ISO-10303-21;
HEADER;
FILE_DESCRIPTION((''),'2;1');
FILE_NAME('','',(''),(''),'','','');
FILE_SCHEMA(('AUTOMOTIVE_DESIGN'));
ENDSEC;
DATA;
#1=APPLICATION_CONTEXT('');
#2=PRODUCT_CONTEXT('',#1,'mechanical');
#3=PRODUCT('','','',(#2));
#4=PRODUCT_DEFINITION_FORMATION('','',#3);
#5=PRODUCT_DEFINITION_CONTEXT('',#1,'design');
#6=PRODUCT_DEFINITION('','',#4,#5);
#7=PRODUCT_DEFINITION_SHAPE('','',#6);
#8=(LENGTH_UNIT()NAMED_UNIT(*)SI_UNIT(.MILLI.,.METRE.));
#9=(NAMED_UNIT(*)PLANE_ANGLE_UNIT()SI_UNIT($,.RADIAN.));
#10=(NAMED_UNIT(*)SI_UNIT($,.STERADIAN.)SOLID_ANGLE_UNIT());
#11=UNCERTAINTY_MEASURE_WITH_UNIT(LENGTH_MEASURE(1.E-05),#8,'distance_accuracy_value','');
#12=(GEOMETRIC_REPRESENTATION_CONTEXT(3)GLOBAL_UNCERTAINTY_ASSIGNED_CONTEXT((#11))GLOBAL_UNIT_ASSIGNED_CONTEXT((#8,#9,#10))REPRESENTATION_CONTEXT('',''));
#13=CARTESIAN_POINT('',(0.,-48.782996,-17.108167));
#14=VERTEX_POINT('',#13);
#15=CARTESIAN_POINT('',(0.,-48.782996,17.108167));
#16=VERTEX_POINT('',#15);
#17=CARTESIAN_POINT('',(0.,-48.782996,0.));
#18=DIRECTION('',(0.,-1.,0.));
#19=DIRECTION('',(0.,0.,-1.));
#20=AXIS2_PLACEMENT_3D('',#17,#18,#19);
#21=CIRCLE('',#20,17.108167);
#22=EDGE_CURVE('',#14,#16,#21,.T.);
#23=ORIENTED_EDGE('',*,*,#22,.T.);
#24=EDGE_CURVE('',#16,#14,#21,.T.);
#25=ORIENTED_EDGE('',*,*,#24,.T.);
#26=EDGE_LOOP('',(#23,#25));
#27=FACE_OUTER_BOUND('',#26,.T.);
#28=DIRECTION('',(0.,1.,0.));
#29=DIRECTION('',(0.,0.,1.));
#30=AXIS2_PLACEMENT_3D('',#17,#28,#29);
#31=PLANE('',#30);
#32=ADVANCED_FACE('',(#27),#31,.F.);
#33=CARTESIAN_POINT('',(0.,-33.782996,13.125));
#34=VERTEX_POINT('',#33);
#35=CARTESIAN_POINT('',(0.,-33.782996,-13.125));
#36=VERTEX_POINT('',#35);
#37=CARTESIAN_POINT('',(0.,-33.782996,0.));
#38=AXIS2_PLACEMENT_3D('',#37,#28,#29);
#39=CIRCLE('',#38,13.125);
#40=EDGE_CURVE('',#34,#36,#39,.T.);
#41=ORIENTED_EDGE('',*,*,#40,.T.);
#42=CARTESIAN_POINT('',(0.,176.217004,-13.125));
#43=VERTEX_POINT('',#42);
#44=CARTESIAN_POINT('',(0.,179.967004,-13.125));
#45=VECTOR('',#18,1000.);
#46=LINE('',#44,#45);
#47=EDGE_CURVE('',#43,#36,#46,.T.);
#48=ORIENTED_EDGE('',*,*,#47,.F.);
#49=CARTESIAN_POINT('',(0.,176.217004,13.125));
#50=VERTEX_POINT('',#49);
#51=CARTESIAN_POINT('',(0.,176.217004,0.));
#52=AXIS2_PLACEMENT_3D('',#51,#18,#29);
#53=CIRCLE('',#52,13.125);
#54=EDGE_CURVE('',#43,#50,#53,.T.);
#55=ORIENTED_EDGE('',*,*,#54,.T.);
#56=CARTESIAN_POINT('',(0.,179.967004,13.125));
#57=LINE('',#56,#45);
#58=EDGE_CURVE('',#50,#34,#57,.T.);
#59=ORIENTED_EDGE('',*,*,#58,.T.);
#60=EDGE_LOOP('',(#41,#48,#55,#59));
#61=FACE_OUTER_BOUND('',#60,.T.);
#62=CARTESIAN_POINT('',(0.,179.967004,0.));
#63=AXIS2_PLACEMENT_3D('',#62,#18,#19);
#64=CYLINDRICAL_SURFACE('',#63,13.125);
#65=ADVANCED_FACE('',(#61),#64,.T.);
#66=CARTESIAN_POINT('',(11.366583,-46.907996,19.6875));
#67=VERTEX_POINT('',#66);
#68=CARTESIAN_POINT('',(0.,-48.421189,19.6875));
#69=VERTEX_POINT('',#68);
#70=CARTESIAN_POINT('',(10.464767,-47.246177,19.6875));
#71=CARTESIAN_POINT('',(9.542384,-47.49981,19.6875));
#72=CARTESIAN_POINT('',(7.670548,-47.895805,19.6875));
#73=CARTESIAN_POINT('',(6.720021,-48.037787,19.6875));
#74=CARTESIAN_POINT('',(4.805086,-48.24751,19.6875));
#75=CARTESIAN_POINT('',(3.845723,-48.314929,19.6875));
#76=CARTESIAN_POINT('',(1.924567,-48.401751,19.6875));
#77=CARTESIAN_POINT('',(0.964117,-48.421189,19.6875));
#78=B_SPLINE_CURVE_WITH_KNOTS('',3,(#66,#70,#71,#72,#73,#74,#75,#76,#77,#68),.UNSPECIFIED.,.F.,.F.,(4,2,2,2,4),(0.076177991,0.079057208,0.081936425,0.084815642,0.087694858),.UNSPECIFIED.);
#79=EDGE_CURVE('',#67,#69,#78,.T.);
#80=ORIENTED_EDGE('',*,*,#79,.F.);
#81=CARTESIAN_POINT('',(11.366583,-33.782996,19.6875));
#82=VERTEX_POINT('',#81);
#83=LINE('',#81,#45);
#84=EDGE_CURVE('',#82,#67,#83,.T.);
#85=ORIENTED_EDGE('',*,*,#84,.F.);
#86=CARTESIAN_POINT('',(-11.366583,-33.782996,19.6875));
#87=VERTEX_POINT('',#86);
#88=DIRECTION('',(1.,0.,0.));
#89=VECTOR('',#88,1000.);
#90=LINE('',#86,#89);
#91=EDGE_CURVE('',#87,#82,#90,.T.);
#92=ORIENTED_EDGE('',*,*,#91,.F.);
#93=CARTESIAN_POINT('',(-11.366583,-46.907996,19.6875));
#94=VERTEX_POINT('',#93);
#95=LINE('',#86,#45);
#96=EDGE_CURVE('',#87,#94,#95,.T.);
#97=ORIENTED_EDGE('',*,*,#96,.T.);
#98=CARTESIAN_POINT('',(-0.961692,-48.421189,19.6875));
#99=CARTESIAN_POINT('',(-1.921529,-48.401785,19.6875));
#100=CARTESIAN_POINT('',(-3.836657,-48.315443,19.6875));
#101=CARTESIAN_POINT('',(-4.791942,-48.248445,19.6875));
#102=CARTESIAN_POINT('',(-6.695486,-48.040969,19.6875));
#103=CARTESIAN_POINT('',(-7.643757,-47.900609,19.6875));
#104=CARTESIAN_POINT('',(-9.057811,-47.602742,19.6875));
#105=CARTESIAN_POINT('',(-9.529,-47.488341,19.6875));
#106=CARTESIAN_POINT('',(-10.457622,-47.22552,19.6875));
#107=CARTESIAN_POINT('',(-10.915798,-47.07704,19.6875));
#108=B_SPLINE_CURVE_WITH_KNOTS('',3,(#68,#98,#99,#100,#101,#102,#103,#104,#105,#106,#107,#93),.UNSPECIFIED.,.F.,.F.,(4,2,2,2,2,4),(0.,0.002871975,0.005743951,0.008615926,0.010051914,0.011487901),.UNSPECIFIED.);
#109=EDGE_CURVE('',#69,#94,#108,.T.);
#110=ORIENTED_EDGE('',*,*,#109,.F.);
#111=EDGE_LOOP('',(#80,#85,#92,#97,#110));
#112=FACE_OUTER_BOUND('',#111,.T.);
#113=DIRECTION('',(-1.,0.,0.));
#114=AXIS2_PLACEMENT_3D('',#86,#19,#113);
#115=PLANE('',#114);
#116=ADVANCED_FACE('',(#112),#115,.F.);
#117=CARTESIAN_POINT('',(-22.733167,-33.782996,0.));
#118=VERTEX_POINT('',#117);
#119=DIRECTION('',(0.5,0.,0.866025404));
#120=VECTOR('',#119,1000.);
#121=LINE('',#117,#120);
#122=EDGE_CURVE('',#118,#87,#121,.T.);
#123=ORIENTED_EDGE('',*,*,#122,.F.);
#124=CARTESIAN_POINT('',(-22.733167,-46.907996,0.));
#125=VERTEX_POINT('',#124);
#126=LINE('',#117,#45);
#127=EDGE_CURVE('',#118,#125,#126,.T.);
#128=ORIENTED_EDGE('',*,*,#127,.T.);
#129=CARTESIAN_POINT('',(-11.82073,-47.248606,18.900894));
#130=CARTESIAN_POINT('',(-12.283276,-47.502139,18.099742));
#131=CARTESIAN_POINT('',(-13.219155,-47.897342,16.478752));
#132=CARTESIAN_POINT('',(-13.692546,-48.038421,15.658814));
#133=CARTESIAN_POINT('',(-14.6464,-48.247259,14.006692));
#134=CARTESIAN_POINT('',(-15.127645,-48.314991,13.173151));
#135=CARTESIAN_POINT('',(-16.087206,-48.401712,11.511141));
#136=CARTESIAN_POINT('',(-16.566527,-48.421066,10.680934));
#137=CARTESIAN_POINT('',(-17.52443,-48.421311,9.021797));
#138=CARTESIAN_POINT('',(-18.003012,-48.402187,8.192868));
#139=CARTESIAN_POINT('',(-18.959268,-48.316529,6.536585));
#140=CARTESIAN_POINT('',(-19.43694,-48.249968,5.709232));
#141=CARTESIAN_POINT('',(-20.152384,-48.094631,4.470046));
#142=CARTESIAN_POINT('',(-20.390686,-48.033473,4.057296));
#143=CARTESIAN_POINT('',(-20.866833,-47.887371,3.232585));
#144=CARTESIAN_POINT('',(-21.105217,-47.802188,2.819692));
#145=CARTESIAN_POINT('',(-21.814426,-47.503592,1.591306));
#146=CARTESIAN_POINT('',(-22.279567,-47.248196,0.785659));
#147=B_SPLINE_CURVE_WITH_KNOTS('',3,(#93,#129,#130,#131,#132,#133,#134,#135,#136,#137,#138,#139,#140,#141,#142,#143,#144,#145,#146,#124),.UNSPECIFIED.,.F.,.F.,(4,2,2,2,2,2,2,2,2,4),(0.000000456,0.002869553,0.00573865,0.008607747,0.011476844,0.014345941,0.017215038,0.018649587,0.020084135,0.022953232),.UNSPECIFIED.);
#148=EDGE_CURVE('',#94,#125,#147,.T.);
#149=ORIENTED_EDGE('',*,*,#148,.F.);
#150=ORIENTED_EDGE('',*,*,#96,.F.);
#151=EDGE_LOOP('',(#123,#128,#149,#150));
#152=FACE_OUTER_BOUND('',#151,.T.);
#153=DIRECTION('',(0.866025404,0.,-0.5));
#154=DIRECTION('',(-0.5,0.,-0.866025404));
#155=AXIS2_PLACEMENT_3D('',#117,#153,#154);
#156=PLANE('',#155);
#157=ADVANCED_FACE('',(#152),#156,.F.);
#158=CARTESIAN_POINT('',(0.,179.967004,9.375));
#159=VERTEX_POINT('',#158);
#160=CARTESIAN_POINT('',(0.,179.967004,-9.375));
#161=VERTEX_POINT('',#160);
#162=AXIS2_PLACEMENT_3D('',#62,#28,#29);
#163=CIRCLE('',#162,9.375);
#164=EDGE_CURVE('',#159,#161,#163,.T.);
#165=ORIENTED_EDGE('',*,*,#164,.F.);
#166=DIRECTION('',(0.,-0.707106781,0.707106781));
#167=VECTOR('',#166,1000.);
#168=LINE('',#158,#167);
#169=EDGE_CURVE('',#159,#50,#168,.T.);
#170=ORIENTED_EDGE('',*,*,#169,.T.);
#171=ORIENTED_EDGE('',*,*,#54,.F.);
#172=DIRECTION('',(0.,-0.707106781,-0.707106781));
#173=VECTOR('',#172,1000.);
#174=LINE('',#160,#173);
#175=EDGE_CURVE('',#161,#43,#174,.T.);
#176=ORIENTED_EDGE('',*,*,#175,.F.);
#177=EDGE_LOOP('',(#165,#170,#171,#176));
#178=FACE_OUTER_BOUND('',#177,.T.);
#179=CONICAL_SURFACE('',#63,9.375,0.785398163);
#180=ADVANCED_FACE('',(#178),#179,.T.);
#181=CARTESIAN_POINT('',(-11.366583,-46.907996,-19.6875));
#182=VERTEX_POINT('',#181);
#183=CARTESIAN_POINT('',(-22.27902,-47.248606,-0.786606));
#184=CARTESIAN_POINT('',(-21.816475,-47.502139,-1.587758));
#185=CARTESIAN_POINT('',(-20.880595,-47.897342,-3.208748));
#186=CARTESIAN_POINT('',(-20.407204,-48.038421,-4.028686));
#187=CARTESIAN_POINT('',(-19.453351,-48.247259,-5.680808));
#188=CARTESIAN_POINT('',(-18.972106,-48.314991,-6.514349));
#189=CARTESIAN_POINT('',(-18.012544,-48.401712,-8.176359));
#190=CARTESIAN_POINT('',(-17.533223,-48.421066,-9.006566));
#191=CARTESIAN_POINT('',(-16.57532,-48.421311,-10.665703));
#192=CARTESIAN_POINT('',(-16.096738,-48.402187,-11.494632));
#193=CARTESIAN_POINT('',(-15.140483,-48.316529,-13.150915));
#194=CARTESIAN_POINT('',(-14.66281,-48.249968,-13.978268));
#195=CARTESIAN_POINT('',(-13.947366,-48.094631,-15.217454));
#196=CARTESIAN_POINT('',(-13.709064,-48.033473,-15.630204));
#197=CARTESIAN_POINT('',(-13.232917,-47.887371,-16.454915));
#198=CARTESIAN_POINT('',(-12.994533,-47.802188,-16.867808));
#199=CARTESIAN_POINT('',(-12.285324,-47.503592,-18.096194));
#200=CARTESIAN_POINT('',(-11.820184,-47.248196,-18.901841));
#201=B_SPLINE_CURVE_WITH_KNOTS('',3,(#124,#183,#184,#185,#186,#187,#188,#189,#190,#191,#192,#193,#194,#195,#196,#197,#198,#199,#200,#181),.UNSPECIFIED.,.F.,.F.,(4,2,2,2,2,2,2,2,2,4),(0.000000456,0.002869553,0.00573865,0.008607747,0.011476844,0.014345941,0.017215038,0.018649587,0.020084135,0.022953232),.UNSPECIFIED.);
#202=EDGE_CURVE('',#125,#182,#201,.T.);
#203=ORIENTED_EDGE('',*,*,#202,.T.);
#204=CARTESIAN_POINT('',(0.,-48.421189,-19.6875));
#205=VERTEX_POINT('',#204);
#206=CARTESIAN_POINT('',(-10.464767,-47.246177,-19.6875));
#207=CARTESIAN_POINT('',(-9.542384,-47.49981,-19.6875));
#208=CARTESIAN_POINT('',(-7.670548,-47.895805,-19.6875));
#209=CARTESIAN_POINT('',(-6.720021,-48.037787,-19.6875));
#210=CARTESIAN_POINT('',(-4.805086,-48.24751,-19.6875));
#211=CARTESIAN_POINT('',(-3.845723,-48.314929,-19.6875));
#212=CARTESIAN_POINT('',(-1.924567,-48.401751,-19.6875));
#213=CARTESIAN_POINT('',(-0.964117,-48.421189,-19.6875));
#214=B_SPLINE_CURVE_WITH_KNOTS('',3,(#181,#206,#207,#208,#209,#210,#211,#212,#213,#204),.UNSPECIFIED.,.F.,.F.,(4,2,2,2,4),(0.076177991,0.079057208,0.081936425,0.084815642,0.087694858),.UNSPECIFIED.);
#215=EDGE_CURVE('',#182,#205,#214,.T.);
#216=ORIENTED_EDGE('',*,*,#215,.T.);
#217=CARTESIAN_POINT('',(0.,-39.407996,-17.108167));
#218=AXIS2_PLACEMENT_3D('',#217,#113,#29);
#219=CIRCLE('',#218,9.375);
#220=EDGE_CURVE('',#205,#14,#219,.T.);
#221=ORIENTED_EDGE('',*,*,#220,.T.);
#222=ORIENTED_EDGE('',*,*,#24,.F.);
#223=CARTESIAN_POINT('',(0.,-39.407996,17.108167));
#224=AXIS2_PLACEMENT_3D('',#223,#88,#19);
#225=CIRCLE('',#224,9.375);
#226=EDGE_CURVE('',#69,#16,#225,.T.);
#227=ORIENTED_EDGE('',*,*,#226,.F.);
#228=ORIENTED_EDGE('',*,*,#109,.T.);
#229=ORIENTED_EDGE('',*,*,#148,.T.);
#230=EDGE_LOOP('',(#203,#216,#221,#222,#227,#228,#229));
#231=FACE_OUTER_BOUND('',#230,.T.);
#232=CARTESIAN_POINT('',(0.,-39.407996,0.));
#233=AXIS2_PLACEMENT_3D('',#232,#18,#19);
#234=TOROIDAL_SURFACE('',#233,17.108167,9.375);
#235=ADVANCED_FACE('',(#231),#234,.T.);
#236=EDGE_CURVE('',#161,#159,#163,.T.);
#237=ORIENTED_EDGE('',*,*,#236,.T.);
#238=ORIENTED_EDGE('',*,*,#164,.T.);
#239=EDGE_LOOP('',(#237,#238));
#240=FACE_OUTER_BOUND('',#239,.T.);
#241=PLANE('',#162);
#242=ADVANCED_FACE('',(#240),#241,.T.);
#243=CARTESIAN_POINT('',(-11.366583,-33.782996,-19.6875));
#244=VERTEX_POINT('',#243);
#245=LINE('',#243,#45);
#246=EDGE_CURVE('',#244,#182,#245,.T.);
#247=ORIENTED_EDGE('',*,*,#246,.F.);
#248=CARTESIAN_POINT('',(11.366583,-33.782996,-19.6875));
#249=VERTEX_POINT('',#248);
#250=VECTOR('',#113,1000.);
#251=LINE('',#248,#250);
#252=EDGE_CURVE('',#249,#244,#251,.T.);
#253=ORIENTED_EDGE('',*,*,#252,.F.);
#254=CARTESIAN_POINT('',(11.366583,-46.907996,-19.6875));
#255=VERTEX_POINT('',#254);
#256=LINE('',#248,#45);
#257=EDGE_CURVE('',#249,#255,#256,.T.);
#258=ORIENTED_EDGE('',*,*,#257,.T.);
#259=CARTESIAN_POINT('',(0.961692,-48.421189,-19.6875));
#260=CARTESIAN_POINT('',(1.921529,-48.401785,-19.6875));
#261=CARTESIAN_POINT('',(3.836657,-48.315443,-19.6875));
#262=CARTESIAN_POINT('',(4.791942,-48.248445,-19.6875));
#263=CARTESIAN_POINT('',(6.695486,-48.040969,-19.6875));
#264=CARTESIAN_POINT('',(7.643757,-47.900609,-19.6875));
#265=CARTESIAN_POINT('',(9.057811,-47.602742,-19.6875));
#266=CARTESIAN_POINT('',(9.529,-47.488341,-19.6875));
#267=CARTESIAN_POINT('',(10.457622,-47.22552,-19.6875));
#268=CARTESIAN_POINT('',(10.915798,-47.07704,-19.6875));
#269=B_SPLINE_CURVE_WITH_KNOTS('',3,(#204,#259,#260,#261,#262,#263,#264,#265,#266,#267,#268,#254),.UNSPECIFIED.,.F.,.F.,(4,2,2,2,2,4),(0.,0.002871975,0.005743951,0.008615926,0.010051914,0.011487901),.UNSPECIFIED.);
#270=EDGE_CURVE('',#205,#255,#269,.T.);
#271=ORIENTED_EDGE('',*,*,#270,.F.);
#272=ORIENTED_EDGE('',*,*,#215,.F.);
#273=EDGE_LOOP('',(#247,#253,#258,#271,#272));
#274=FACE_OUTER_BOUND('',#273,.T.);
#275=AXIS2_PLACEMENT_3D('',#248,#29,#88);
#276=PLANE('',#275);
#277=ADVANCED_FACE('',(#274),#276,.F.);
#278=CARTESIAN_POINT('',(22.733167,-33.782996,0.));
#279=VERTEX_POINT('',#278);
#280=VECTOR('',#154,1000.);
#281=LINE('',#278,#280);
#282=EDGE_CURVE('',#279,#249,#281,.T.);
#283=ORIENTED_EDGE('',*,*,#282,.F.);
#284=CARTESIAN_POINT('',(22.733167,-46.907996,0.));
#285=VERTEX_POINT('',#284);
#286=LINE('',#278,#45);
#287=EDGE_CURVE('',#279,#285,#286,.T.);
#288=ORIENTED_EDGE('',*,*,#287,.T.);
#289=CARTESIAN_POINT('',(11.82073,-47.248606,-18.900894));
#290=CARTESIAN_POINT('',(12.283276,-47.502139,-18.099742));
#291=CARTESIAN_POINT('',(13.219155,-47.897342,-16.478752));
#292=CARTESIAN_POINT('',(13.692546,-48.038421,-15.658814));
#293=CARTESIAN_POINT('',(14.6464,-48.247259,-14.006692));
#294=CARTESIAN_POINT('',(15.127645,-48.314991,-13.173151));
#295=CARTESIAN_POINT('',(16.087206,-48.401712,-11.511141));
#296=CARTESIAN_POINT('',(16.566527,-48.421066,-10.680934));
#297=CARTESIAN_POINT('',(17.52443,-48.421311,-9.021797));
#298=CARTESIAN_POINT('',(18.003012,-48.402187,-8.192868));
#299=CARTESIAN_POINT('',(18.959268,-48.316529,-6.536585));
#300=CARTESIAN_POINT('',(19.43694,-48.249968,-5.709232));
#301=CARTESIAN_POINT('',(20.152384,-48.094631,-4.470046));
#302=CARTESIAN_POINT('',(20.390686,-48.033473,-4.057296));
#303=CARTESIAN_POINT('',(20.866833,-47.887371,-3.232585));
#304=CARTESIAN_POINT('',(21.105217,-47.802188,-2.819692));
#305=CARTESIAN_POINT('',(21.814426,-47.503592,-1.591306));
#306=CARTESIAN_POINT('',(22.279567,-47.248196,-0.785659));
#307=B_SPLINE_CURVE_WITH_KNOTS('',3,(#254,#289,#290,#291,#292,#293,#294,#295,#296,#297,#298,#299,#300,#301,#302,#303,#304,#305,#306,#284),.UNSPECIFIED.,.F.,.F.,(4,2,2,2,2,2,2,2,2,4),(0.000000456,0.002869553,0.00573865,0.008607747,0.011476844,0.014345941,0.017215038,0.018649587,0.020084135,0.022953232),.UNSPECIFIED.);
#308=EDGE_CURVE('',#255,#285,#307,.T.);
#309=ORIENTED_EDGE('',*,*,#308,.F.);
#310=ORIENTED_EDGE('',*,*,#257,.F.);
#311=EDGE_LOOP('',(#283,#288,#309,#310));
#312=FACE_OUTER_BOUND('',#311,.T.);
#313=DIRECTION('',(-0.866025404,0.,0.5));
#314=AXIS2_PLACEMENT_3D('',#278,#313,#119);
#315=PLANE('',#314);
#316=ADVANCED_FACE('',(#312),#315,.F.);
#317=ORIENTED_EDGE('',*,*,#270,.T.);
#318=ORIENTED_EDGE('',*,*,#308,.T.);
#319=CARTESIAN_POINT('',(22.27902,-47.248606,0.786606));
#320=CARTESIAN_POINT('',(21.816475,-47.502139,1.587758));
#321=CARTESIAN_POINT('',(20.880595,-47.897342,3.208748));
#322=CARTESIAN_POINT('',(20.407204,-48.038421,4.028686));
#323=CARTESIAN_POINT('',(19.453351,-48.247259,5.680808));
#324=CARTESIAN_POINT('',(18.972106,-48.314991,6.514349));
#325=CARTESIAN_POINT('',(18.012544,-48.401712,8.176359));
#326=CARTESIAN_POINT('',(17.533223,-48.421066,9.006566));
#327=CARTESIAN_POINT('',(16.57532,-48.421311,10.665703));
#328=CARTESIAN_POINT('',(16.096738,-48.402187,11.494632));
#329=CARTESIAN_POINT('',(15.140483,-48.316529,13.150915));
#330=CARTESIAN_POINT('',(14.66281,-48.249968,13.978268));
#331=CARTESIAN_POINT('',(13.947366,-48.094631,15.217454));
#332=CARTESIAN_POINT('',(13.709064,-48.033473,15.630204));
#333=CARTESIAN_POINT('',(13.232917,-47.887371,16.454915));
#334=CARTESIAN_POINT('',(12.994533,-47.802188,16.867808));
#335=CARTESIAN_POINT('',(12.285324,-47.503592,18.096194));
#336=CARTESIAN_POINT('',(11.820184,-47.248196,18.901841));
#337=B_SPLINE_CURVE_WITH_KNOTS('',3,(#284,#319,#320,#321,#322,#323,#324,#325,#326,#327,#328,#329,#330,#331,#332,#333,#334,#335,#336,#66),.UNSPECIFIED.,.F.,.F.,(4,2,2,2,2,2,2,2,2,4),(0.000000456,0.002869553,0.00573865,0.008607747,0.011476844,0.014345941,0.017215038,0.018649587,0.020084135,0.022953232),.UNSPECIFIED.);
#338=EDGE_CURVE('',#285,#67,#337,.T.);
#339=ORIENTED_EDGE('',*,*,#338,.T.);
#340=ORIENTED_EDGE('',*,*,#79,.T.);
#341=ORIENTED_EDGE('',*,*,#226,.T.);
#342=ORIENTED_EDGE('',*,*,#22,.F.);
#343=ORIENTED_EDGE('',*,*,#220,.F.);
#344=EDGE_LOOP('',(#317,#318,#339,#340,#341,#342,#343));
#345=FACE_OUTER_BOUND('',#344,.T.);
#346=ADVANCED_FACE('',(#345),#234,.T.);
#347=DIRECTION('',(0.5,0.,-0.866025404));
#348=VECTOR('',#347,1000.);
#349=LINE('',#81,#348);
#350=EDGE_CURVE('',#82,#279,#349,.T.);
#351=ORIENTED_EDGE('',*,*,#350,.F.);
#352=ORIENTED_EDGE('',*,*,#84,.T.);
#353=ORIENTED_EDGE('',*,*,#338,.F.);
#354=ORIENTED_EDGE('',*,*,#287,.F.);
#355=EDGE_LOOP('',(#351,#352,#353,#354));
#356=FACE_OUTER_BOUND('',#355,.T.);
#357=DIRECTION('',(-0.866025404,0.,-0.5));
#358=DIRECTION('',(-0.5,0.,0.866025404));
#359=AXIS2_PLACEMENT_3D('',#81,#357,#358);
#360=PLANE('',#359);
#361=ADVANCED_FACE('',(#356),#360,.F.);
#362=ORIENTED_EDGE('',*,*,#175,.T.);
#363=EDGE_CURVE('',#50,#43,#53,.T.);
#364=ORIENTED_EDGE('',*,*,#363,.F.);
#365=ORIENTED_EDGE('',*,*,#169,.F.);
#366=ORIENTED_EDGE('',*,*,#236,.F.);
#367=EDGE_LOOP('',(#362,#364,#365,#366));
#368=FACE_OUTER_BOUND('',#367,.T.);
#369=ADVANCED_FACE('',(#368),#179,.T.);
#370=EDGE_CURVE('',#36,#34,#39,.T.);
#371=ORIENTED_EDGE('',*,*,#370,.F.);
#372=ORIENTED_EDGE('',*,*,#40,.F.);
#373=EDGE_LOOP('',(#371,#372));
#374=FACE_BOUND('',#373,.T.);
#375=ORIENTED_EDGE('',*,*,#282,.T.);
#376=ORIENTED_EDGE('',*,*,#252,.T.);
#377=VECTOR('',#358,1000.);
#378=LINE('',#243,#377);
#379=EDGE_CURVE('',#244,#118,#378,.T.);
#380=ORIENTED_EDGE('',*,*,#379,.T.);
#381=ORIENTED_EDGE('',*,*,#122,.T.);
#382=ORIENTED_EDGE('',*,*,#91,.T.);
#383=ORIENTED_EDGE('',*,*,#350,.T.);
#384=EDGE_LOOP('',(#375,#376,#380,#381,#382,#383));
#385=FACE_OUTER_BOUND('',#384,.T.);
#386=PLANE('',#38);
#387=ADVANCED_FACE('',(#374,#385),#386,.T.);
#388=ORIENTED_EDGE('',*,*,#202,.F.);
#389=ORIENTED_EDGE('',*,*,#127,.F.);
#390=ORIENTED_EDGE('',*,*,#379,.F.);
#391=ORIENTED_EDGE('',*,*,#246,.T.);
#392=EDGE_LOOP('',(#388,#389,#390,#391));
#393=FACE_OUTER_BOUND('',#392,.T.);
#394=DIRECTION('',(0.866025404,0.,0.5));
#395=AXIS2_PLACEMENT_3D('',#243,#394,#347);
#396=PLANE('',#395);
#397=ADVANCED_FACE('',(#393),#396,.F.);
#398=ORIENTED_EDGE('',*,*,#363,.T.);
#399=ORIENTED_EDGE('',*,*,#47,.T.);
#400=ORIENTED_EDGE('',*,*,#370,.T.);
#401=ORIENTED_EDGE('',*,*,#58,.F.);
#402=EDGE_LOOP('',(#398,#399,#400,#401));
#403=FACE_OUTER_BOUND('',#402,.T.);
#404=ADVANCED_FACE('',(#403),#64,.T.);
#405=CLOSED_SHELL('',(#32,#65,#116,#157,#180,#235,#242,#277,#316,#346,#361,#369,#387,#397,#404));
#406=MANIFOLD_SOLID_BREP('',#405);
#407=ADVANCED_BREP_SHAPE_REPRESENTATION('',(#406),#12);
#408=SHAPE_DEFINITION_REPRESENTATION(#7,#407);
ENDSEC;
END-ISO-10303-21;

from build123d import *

# Parameters (mm, degrees)
BOSS_EXTRUDE1_DEPTH = 8
SKETCH2_R           = 7
BOSS_EXTRUDE2_DEPTH = 114
CHAMFER1_SIZE       = 2
SCALE_1_SCALE       = 1.875


with BuildPart() as part:
    # Sketch1 → Boss-Extrude1 (new body)
    with BuildSketch(Plane(origin=(0, 0, 0), x_dir=(1, 0, 0), z_dir=(0, 1, 0))):
        Polygon((12.124355653, 0), (6.062177826, 10.5), (-6.062177826, 10.5), (-12.124355653, 0), (-6.062177826, -10.5), (6.062177826, -10.5), align=None)
    extrude(amount=BOSS_EXTRUDE1_DEPTH)

    # Sketch2 → Boss-Extrude2 (add)
    with BuildSketch(Plane(origin=(0, 8, 0), x_dir=(1, 0, 0), z_dir=(0, 1, 0))):
        with Locations(Location((0, 0, 0), (0, 0, 90))):
            Circle(SKETCH2_R)
    extrude(amount=BOSS_EXTRUDE2_DEPTH)

    # Chamfer1
    chamfer1_edges = [part.edges().sort_by_distance(p)[0] for p in [
        (0, 122, 7),
    ]]
    chamfer(chamfer1_edges, length=CHAMFER1_SIZE)

    # Sketch3 → Cut-Revolve1 (revolve, cut)
    with BuildSketch(Plane.XY, mode=Mode.PRIVATE) as cut_revolve1_sk:
        with BuildLine():
            Line((-12.124355653, 0), (-12.124355653, 1))
            ThreePointArc((-12.124355653, 1), (-10.705494483, 0.25658351), (-9.124355653, 0))
            Line((-9.124355653, 0), (-12.124355653, 0))
        make_face()
    revolve(cut_revolve1_sk.sketch.rotate(Axis((0, 0, 0), (0, 1, 0)), 270), axis=Axis((0, 0, 0), (0, 1, 0)), mode=Mode.SUBTRACT)


with BuildPart() as part_1:
    # Scale 1: scaled about (-1.43e-07, 55.752743575, -2.4e-08)
    add(part.part.scale(SCALE_1_SCALE).moved(Location((1.25e-07, -48.783650628, 2.1e-08))))


solid = part_1.part
